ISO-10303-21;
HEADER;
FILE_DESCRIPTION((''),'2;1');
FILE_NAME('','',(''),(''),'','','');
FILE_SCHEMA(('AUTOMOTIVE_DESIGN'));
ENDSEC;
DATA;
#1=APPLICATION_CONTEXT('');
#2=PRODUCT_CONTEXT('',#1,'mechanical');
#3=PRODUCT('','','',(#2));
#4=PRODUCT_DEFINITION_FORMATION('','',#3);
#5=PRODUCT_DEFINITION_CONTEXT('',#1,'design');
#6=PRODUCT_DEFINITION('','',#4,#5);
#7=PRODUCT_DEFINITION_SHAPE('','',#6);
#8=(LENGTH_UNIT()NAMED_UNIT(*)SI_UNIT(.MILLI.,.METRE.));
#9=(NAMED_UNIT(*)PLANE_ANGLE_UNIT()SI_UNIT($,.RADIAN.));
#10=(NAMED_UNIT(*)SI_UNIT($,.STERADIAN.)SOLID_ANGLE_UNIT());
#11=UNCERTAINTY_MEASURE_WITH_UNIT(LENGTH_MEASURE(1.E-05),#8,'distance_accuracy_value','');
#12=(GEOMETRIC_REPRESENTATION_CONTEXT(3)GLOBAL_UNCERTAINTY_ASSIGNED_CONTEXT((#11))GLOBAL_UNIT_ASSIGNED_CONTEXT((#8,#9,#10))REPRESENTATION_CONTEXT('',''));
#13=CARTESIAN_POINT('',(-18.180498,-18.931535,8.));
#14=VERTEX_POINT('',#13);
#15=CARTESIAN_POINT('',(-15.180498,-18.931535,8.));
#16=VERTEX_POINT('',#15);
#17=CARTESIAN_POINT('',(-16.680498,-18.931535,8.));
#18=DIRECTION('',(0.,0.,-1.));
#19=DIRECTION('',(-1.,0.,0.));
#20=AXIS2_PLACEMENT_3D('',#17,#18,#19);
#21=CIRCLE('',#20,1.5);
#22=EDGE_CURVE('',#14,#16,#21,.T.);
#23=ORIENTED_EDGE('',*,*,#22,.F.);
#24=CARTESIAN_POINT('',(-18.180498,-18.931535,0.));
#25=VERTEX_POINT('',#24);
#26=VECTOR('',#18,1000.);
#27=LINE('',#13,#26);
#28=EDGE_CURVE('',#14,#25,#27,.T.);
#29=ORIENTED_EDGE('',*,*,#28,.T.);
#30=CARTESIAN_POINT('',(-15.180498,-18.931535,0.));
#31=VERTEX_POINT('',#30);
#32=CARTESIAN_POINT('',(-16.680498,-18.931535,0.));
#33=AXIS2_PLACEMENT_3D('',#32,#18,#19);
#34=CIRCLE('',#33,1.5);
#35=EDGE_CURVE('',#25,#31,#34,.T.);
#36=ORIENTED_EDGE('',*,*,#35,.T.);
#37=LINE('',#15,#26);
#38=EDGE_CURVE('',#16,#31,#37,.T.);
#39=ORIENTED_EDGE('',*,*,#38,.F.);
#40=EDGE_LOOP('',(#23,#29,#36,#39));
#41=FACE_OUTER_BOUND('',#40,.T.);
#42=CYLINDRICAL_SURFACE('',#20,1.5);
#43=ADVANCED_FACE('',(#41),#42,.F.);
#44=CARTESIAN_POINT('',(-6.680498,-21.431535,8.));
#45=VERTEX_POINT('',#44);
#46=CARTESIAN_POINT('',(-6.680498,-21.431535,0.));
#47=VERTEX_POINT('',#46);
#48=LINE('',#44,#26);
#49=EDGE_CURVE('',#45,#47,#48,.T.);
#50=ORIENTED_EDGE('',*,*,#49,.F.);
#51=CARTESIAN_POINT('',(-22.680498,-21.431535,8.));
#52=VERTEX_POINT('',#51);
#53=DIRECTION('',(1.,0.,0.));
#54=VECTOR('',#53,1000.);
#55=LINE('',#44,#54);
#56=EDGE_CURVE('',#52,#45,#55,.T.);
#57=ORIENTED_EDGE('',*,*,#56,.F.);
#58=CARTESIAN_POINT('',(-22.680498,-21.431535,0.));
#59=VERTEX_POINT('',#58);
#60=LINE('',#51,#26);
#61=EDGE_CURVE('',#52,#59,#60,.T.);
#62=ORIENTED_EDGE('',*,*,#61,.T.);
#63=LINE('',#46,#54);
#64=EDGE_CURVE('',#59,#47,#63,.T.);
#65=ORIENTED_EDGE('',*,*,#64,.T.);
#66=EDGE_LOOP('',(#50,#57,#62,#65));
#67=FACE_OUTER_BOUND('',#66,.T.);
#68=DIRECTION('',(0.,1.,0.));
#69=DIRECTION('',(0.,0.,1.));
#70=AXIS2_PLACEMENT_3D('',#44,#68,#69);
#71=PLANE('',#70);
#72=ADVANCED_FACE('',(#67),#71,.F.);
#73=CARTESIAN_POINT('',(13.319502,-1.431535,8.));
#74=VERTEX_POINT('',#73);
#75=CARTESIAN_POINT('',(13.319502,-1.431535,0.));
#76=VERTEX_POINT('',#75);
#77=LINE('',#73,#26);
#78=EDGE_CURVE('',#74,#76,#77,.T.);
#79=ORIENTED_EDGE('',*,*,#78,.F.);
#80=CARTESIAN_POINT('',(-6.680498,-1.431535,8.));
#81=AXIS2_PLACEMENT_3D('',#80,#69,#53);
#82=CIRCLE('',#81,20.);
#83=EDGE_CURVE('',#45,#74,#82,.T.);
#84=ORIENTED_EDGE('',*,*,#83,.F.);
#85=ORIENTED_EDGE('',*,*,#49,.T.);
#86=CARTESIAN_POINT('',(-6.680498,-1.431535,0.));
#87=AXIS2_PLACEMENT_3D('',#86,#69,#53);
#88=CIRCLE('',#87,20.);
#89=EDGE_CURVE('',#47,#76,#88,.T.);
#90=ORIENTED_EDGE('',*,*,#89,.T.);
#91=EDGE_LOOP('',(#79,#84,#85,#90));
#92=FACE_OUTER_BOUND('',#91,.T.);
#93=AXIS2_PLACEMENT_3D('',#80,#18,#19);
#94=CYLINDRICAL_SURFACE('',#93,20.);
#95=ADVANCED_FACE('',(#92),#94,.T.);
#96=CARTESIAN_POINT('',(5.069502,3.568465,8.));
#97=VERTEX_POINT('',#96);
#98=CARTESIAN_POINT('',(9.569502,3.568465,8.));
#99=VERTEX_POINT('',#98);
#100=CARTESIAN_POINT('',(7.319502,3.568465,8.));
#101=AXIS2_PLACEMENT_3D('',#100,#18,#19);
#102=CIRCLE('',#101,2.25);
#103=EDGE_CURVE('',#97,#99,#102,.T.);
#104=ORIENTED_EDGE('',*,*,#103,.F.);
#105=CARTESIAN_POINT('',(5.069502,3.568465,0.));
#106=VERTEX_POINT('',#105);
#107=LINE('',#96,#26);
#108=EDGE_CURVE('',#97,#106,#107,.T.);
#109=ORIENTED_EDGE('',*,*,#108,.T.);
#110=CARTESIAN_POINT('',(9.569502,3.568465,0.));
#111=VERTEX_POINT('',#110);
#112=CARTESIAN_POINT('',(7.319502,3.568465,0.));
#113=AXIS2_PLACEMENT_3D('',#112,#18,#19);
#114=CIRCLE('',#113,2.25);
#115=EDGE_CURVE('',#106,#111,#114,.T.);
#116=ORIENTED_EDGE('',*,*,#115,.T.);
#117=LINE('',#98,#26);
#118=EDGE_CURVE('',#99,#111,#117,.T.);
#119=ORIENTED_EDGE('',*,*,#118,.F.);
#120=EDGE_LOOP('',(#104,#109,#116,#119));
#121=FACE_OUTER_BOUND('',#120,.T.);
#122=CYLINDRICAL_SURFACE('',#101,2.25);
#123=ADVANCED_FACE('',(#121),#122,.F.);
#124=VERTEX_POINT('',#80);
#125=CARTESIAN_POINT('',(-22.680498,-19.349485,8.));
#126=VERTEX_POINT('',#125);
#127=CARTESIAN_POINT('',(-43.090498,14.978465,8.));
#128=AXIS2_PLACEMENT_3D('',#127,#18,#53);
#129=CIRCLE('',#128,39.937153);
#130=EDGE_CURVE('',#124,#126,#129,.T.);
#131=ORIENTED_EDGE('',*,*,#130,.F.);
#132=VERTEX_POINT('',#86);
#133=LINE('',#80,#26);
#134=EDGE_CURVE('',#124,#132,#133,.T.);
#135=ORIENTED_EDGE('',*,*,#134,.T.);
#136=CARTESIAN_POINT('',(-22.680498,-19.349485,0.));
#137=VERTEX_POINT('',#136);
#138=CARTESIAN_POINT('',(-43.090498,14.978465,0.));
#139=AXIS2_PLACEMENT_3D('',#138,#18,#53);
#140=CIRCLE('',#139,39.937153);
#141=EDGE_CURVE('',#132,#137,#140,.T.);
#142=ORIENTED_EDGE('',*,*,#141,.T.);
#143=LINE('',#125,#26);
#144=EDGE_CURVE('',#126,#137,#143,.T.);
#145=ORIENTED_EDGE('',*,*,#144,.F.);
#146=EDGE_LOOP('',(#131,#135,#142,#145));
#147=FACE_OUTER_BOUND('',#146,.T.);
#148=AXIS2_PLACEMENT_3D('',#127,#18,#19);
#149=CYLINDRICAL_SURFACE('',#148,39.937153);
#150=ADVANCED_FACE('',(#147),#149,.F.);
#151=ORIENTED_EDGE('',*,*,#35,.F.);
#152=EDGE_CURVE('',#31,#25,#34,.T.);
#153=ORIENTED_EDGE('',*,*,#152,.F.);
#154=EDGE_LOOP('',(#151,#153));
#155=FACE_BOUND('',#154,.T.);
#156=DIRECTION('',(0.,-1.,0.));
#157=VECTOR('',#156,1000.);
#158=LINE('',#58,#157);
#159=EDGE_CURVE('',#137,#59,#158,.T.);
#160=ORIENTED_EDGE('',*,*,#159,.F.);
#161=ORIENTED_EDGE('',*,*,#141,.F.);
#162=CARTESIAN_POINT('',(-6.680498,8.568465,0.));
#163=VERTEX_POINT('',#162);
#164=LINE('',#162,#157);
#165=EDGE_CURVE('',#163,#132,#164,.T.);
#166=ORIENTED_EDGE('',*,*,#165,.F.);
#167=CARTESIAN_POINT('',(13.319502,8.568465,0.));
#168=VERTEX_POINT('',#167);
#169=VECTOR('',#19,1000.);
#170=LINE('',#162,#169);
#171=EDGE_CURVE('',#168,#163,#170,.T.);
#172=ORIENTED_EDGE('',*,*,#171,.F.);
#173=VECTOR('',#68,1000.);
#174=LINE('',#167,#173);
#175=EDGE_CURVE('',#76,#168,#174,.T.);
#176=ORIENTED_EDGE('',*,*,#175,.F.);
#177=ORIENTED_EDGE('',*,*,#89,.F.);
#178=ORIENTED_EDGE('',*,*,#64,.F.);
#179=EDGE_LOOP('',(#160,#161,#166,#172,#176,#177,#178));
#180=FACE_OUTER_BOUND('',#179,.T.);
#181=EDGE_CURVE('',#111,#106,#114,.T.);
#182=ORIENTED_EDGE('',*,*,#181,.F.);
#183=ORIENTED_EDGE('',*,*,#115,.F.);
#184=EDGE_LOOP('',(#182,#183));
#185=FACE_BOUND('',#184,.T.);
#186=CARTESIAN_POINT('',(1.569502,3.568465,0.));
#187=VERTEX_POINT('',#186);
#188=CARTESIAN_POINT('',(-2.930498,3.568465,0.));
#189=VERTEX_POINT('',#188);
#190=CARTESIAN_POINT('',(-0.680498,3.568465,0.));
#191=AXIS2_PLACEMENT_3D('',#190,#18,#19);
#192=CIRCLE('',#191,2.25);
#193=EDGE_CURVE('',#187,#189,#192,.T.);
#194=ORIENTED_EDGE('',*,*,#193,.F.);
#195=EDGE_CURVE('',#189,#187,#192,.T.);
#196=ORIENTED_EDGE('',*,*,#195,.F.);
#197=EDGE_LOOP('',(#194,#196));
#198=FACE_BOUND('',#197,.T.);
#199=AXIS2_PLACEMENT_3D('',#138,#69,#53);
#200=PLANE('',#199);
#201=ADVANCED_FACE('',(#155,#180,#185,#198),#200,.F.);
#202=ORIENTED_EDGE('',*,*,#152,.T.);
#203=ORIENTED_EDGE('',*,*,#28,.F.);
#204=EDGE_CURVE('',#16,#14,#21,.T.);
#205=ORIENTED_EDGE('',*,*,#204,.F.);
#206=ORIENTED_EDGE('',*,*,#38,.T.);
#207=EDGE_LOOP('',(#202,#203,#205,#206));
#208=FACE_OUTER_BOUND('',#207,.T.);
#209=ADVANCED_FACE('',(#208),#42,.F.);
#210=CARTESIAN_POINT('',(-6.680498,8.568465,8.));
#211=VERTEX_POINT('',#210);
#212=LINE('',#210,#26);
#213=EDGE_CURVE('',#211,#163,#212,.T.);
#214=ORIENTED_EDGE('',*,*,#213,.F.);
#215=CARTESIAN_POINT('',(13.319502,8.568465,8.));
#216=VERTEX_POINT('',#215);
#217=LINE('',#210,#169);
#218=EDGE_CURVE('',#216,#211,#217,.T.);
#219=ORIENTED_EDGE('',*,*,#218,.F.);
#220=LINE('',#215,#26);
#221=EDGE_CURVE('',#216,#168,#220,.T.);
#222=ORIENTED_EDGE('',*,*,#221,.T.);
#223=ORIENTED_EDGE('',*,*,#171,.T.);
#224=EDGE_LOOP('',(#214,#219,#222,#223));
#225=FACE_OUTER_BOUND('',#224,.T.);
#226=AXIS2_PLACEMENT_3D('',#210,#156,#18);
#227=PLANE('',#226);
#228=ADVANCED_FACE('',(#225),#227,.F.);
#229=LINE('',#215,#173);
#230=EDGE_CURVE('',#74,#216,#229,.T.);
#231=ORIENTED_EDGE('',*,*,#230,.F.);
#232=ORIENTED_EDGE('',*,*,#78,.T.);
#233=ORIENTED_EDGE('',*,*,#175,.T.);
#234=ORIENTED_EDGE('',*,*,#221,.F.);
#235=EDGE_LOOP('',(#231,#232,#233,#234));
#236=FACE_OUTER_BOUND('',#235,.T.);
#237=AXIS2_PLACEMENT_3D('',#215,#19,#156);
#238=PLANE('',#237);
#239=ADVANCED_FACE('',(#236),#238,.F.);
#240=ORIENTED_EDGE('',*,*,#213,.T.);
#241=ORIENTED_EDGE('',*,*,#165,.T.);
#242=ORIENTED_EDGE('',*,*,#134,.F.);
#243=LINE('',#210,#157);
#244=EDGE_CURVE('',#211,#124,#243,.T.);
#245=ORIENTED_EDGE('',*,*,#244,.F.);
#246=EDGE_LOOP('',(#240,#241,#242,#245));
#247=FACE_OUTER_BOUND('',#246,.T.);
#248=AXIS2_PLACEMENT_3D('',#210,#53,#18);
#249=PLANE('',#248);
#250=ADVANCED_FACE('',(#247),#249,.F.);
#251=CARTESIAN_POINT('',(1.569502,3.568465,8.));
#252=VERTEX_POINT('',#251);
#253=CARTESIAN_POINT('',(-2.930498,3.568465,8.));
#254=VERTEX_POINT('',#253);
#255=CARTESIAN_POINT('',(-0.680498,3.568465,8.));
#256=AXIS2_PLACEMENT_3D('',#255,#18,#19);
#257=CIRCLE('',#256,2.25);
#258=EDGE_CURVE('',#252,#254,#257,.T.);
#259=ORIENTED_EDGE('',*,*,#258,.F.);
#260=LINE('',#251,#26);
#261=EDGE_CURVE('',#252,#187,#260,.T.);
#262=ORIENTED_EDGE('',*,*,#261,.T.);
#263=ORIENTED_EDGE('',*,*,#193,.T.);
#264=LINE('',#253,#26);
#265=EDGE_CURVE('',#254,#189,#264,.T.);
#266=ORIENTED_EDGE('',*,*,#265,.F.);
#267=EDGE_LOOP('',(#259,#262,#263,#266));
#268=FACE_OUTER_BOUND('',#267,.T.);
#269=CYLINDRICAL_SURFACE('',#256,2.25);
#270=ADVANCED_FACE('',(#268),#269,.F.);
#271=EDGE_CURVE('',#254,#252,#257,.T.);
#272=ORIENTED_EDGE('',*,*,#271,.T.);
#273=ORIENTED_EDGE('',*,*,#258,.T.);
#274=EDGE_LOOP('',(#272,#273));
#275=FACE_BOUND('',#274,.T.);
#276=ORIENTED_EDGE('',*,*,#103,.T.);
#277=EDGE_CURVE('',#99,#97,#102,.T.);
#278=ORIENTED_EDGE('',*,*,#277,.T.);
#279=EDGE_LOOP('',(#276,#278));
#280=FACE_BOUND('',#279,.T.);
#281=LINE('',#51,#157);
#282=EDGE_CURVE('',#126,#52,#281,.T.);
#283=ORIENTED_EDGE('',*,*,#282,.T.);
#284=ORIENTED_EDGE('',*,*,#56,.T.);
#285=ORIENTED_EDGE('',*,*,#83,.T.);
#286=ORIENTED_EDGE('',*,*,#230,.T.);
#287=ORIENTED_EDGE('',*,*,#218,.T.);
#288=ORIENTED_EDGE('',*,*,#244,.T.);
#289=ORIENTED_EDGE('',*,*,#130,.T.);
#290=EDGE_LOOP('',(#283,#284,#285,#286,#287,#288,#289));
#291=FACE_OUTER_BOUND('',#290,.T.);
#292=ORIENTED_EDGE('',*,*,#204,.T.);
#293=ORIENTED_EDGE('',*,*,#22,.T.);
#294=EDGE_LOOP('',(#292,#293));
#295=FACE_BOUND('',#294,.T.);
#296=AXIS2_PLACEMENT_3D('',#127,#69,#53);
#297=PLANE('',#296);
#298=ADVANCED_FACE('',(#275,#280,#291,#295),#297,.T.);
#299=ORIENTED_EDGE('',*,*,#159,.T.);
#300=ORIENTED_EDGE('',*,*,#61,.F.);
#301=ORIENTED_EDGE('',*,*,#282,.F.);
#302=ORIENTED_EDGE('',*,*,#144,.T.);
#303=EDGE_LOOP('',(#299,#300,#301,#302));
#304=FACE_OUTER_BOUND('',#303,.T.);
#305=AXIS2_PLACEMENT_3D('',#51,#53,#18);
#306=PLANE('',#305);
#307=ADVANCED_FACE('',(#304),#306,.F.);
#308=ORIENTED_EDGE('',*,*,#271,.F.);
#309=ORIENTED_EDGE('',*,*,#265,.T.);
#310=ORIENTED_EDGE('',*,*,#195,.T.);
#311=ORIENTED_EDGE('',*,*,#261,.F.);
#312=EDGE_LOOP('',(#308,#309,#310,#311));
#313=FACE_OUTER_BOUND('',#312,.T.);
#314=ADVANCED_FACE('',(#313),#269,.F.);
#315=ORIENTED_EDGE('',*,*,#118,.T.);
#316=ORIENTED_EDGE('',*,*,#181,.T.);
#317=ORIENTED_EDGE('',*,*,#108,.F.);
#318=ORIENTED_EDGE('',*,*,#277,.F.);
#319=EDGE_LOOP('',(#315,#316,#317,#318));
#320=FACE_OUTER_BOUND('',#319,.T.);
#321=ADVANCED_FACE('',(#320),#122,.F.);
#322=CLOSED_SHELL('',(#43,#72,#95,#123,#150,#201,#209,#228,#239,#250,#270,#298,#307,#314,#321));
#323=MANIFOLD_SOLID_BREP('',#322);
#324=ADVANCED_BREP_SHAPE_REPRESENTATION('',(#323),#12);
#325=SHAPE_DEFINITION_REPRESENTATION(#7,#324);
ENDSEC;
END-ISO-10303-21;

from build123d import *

# Parameters (mm, degrees)
EXTRUDE_1_DEPTH     = 8
SKETCH_2_R          = 1.5
SKETCH_2_R_2        = 2.25
CUT_EXTRUDE_1_DEPTH = 33.213594803


with BuildPart() as part:
    # 草图1 → 凸台-拉伸1 (new body)
    with BuildSketch(Plane.XY):
        with BuildLine():
            Line((-6.680497925, 8.56846473), (13.319502075, 8.56846473))
            Line((13.319502075, 8.56846473), (13.319502075, -1.43153527))
            ThreePointArc((13.319502075, -1.43153527), (7.461637698, -15.573670893), (-6.680497925, -21.43153527))
            Line((-6.680497925, -21.43153527), (-22.680497925, -21.43153527))
            Line((-22.680497925, -21.43153527), (-22.680497925, -19.349484524))
            ThreePointArc((-22.680497925, -19.349484524), (-13.301383699, -11.622002815), (-6.680497925, -1.43153527))
            Line((-6.680497925, -1.43153527), (-6.680497925, 8.56846473))
        make_face()
    extrude(amount=EXTRUDE_1_DEPTH)

    # 草图2 → 切除-拉伸1 (cut, through all)
    with BuildSketch(Plane(origin=(0, 0, 0), x_dir=(-1, 0, 0), z_dir=(0, 0, -1))):
        with Locations((16.680497925, -18.93153527)):
            Circle(SKETCH_2_R)
        with Locations((0.680497925, 3.56846473)):
            Circle(SKETCH_2_R_2)
        with Locations((-7.319502075, 3.56846473)):
            Circle(SKETCH_2_R_2)
    extrude(amount=-CUT_EXTRUDE_1_DEPTH, mode=Mode.SUBTRACT)


solid = part.part
